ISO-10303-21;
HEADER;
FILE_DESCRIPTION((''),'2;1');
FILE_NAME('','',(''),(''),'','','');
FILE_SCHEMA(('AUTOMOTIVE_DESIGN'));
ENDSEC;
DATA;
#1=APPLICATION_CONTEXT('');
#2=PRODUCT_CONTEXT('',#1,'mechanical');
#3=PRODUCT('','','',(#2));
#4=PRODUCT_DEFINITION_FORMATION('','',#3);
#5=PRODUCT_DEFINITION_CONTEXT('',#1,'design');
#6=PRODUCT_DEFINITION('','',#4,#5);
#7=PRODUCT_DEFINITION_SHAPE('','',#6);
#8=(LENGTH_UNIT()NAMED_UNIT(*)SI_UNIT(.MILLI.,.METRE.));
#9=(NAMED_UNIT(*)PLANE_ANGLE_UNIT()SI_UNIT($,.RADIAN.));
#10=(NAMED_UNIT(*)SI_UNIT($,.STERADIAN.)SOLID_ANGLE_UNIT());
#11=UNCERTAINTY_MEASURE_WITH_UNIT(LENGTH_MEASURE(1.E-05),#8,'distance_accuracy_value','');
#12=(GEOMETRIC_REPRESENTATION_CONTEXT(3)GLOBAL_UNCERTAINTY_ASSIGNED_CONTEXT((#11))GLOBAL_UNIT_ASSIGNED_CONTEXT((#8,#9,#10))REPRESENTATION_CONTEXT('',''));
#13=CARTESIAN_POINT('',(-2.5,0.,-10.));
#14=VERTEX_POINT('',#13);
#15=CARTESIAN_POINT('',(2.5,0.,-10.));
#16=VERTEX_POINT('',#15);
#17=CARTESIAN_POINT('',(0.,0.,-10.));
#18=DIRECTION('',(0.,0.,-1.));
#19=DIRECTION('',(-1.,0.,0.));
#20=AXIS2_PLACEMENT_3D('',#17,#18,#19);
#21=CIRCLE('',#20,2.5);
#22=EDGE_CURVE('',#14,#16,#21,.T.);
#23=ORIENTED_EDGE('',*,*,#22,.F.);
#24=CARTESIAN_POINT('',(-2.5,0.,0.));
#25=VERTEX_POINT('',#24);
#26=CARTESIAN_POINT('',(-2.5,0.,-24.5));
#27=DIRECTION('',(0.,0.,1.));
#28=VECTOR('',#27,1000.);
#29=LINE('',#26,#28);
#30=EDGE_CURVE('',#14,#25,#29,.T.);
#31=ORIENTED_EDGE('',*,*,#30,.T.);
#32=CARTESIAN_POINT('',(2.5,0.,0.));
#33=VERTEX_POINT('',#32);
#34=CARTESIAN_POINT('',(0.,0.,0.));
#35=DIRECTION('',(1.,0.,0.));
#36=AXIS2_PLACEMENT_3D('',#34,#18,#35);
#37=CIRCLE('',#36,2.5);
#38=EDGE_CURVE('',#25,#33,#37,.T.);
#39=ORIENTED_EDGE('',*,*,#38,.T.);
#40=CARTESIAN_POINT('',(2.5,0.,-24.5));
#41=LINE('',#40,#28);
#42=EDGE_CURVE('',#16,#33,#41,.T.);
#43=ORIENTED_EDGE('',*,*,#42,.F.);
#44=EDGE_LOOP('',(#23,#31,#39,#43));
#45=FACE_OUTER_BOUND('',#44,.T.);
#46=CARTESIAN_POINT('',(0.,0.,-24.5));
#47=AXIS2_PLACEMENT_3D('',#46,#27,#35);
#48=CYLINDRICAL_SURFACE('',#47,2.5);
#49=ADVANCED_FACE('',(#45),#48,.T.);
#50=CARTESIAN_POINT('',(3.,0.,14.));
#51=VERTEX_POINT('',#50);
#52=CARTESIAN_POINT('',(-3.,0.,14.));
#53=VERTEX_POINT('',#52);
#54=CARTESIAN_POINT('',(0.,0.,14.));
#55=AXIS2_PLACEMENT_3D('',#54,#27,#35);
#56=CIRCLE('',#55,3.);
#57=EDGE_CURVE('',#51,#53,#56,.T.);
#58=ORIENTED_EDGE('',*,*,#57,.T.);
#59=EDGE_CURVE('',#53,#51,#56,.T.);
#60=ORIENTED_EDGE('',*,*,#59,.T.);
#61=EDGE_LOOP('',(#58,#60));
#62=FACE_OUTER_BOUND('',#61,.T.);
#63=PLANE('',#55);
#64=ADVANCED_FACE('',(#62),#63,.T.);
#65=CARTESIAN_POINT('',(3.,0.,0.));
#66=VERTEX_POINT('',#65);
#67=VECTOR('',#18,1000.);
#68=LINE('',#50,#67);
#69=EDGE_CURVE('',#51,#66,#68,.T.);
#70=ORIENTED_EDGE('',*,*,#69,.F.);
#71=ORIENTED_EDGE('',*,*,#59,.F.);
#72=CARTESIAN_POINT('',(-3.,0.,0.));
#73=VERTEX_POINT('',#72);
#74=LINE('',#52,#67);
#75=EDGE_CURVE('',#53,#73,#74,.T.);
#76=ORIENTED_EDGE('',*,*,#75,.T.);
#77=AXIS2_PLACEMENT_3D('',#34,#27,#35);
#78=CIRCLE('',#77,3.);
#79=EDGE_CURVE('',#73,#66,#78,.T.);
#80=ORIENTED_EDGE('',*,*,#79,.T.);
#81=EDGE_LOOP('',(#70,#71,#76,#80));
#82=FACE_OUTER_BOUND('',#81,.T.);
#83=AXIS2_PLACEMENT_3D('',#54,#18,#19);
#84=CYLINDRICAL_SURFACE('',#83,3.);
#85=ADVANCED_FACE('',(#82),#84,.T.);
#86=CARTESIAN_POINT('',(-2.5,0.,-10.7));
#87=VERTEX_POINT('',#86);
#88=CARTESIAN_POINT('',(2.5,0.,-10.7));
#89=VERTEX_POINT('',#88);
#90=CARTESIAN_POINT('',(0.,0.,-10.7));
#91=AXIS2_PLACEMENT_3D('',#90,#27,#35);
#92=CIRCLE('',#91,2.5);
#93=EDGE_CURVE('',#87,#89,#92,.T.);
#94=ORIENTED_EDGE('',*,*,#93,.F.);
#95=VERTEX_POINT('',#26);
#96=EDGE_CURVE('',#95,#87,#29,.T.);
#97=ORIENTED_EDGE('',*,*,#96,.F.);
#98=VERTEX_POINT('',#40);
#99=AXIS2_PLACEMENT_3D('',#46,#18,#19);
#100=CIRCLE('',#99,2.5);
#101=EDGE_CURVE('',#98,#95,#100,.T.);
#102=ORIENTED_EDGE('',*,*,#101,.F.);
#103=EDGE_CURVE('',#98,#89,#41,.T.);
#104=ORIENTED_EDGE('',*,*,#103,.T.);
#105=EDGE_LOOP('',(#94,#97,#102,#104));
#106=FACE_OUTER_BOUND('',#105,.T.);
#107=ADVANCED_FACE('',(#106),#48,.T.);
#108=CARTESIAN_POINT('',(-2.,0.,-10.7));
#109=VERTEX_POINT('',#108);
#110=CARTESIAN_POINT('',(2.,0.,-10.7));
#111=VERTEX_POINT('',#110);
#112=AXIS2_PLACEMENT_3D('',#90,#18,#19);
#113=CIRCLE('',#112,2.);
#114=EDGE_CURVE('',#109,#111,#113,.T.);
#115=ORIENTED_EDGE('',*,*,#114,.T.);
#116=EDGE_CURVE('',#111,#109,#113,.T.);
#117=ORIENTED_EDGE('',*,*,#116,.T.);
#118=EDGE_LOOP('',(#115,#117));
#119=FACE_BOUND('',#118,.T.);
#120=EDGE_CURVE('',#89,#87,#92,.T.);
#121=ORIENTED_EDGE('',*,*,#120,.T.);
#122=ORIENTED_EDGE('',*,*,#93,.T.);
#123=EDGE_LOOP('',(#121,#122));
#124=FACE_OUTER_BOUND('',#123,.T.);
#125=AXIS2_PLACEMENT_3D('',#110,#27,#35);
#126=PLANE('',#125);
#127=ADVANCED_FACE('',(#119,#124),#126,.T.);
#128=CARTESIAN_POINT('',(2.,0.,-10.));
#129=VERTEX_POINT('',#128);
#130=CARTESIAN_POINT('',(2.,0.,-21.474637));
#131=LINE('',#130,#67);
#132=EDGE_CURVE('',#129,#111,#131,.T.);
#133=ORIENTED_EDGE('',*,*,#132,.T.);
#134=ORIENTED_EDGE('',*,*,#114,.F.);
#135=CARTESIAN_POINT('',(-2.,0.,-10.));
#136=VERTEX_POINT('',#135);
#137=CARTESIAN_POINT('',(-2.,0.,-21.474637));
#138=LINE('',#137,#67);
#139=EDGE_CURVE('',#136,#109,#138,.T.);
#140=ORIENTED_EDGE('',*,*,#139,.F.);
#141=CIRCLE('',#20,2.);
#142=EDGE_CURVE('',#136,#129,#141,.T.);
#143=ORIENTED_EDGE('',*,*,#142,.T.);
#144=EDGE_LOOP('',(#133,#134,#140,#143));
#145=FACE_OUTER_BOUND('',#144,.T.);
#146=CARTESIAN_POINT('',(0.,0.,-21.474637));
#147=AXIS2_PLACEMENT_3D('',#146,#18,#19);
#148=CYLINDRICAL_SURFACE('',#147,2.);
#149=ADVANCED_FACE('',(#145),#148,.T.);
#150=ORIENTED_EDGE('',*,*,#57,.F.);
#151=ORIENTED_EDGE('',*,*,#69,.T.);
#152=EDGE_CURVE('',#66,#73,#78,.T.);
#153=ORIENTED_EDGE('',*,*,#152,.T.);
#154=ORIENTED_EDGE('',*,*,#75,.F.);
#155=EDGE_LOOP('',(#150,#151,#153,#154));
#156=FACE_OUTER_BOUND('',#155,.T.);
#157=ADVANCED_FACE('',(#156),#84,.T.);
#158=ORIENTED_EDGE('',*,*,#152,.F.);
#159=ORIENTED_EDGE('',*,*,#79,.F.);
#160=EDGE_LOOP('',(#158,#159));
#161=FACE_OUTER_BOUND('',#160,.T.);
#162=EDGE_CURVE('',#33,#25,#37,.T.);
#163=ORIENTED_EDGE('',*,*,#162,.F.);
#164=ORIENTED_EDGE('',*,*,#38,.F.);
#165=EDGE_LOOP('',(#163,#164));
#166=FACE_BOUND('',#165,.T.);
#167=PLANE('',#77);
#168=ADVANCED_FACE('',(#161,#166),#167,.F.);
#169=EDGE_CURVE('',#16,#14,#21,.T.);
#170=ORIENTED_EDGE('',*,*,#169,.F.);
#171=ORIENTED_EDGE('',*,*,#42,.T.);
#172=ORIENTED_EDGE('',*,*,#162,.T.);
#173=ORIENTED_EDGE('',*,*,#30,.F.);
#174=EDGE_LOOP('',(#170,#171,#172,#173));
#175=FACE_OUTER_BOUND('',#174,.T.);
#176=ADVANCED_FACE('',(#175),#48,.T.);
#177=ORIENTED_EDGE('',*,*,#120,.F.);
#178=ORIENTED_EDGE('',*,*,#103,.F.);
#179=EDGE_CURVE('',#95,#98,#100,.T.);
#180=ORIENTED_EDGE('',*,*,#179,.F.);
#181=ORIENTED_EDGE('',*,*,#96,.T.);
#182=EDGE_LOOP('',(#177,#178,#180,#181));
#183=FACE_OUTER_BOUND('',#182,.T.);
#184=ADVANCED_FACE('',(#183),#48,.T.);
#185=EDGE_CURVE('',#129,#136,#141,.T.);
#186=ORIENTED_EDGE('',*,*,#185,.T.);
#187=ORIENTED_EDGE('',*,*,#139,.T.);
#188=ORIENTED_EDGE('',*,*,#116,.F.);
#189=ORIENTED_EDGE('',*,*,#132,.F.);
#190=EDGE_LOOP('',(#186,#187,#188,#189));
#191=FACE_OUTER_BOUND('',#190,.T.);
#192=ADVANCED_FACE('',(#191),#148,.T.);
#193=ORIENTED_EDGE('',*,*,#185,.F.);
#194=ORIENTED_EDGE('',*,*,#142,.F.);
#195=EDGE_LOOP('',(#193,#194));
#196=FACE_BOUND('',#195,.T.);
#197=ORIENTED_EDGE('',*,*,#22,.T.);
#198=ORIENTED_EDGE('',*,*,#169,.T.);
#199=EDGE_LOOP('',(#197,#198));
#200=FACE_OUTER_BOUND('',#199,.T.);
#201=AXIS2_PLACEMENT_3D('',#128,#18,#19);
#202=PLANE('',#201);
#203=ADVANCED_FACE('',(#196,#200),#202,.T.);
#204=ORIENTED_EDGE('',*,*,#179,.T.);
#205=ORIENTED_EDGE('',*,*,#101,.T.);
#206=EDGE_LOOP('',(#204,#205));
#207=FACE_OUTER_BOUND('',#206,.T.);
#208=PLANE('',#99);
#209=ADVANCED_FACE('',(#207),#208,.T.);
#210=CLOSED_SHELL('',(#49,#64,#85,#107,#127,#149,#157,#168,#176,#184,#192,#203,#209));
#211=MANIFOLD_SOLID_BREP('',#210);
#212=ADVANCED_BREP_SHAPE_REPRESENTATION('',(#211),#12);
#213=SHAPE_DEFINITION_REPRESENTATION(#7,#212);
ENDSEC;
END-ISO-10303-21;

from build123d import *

# Parameters (mm, degrees)
SKETCH_1_R      = 3
EXTRUDE_1_DEPTH = 14
SKETCH_2_R      = 2.5
EXTRUDE_2_DEPTH = 24.5
SKETCH_3_W      = 1.981719741
SKETCH_3_H      = 0.7


with BuildPart() as part:
    # 草图1 → 凸台-拉伸1 (new body)
    with BuildSketch(Plane.XY):
        Circle(SKETCH_1_R)
    extrude(amount=EXTRUDE_1_DEPTH)

    # 草图2 → 凸台-拉伸2 (add)
    with BuildSketch(Plane(origin=(0, 0, 0), x_dir=(-1, 0, 0), z_dir=(0, 0, -1))):
        with Locations(Location((0, 0, 0), (0, 0, 180))):
            Circle(SKETCH_2_R)
    extrude(amount=EXTRUDE_2_DEPTH)

    # 草图3 → 切除-旋转1 (revolve, cut)
    with BuildSketch(Plane(origin=(0, 0, 0), x_dir=(1, 0, 0), z_dir=(0, 1, 0))):
        with Locations((2.990859871, 10.35)):
            Rectangle(SKETCH_3_W, SKETCH_3_H)
    revolve(axis=Axis((0, 0, -21.474636763), (0, 0, 1)), mode=Mode.SUBTRACT)


solid = part.part
